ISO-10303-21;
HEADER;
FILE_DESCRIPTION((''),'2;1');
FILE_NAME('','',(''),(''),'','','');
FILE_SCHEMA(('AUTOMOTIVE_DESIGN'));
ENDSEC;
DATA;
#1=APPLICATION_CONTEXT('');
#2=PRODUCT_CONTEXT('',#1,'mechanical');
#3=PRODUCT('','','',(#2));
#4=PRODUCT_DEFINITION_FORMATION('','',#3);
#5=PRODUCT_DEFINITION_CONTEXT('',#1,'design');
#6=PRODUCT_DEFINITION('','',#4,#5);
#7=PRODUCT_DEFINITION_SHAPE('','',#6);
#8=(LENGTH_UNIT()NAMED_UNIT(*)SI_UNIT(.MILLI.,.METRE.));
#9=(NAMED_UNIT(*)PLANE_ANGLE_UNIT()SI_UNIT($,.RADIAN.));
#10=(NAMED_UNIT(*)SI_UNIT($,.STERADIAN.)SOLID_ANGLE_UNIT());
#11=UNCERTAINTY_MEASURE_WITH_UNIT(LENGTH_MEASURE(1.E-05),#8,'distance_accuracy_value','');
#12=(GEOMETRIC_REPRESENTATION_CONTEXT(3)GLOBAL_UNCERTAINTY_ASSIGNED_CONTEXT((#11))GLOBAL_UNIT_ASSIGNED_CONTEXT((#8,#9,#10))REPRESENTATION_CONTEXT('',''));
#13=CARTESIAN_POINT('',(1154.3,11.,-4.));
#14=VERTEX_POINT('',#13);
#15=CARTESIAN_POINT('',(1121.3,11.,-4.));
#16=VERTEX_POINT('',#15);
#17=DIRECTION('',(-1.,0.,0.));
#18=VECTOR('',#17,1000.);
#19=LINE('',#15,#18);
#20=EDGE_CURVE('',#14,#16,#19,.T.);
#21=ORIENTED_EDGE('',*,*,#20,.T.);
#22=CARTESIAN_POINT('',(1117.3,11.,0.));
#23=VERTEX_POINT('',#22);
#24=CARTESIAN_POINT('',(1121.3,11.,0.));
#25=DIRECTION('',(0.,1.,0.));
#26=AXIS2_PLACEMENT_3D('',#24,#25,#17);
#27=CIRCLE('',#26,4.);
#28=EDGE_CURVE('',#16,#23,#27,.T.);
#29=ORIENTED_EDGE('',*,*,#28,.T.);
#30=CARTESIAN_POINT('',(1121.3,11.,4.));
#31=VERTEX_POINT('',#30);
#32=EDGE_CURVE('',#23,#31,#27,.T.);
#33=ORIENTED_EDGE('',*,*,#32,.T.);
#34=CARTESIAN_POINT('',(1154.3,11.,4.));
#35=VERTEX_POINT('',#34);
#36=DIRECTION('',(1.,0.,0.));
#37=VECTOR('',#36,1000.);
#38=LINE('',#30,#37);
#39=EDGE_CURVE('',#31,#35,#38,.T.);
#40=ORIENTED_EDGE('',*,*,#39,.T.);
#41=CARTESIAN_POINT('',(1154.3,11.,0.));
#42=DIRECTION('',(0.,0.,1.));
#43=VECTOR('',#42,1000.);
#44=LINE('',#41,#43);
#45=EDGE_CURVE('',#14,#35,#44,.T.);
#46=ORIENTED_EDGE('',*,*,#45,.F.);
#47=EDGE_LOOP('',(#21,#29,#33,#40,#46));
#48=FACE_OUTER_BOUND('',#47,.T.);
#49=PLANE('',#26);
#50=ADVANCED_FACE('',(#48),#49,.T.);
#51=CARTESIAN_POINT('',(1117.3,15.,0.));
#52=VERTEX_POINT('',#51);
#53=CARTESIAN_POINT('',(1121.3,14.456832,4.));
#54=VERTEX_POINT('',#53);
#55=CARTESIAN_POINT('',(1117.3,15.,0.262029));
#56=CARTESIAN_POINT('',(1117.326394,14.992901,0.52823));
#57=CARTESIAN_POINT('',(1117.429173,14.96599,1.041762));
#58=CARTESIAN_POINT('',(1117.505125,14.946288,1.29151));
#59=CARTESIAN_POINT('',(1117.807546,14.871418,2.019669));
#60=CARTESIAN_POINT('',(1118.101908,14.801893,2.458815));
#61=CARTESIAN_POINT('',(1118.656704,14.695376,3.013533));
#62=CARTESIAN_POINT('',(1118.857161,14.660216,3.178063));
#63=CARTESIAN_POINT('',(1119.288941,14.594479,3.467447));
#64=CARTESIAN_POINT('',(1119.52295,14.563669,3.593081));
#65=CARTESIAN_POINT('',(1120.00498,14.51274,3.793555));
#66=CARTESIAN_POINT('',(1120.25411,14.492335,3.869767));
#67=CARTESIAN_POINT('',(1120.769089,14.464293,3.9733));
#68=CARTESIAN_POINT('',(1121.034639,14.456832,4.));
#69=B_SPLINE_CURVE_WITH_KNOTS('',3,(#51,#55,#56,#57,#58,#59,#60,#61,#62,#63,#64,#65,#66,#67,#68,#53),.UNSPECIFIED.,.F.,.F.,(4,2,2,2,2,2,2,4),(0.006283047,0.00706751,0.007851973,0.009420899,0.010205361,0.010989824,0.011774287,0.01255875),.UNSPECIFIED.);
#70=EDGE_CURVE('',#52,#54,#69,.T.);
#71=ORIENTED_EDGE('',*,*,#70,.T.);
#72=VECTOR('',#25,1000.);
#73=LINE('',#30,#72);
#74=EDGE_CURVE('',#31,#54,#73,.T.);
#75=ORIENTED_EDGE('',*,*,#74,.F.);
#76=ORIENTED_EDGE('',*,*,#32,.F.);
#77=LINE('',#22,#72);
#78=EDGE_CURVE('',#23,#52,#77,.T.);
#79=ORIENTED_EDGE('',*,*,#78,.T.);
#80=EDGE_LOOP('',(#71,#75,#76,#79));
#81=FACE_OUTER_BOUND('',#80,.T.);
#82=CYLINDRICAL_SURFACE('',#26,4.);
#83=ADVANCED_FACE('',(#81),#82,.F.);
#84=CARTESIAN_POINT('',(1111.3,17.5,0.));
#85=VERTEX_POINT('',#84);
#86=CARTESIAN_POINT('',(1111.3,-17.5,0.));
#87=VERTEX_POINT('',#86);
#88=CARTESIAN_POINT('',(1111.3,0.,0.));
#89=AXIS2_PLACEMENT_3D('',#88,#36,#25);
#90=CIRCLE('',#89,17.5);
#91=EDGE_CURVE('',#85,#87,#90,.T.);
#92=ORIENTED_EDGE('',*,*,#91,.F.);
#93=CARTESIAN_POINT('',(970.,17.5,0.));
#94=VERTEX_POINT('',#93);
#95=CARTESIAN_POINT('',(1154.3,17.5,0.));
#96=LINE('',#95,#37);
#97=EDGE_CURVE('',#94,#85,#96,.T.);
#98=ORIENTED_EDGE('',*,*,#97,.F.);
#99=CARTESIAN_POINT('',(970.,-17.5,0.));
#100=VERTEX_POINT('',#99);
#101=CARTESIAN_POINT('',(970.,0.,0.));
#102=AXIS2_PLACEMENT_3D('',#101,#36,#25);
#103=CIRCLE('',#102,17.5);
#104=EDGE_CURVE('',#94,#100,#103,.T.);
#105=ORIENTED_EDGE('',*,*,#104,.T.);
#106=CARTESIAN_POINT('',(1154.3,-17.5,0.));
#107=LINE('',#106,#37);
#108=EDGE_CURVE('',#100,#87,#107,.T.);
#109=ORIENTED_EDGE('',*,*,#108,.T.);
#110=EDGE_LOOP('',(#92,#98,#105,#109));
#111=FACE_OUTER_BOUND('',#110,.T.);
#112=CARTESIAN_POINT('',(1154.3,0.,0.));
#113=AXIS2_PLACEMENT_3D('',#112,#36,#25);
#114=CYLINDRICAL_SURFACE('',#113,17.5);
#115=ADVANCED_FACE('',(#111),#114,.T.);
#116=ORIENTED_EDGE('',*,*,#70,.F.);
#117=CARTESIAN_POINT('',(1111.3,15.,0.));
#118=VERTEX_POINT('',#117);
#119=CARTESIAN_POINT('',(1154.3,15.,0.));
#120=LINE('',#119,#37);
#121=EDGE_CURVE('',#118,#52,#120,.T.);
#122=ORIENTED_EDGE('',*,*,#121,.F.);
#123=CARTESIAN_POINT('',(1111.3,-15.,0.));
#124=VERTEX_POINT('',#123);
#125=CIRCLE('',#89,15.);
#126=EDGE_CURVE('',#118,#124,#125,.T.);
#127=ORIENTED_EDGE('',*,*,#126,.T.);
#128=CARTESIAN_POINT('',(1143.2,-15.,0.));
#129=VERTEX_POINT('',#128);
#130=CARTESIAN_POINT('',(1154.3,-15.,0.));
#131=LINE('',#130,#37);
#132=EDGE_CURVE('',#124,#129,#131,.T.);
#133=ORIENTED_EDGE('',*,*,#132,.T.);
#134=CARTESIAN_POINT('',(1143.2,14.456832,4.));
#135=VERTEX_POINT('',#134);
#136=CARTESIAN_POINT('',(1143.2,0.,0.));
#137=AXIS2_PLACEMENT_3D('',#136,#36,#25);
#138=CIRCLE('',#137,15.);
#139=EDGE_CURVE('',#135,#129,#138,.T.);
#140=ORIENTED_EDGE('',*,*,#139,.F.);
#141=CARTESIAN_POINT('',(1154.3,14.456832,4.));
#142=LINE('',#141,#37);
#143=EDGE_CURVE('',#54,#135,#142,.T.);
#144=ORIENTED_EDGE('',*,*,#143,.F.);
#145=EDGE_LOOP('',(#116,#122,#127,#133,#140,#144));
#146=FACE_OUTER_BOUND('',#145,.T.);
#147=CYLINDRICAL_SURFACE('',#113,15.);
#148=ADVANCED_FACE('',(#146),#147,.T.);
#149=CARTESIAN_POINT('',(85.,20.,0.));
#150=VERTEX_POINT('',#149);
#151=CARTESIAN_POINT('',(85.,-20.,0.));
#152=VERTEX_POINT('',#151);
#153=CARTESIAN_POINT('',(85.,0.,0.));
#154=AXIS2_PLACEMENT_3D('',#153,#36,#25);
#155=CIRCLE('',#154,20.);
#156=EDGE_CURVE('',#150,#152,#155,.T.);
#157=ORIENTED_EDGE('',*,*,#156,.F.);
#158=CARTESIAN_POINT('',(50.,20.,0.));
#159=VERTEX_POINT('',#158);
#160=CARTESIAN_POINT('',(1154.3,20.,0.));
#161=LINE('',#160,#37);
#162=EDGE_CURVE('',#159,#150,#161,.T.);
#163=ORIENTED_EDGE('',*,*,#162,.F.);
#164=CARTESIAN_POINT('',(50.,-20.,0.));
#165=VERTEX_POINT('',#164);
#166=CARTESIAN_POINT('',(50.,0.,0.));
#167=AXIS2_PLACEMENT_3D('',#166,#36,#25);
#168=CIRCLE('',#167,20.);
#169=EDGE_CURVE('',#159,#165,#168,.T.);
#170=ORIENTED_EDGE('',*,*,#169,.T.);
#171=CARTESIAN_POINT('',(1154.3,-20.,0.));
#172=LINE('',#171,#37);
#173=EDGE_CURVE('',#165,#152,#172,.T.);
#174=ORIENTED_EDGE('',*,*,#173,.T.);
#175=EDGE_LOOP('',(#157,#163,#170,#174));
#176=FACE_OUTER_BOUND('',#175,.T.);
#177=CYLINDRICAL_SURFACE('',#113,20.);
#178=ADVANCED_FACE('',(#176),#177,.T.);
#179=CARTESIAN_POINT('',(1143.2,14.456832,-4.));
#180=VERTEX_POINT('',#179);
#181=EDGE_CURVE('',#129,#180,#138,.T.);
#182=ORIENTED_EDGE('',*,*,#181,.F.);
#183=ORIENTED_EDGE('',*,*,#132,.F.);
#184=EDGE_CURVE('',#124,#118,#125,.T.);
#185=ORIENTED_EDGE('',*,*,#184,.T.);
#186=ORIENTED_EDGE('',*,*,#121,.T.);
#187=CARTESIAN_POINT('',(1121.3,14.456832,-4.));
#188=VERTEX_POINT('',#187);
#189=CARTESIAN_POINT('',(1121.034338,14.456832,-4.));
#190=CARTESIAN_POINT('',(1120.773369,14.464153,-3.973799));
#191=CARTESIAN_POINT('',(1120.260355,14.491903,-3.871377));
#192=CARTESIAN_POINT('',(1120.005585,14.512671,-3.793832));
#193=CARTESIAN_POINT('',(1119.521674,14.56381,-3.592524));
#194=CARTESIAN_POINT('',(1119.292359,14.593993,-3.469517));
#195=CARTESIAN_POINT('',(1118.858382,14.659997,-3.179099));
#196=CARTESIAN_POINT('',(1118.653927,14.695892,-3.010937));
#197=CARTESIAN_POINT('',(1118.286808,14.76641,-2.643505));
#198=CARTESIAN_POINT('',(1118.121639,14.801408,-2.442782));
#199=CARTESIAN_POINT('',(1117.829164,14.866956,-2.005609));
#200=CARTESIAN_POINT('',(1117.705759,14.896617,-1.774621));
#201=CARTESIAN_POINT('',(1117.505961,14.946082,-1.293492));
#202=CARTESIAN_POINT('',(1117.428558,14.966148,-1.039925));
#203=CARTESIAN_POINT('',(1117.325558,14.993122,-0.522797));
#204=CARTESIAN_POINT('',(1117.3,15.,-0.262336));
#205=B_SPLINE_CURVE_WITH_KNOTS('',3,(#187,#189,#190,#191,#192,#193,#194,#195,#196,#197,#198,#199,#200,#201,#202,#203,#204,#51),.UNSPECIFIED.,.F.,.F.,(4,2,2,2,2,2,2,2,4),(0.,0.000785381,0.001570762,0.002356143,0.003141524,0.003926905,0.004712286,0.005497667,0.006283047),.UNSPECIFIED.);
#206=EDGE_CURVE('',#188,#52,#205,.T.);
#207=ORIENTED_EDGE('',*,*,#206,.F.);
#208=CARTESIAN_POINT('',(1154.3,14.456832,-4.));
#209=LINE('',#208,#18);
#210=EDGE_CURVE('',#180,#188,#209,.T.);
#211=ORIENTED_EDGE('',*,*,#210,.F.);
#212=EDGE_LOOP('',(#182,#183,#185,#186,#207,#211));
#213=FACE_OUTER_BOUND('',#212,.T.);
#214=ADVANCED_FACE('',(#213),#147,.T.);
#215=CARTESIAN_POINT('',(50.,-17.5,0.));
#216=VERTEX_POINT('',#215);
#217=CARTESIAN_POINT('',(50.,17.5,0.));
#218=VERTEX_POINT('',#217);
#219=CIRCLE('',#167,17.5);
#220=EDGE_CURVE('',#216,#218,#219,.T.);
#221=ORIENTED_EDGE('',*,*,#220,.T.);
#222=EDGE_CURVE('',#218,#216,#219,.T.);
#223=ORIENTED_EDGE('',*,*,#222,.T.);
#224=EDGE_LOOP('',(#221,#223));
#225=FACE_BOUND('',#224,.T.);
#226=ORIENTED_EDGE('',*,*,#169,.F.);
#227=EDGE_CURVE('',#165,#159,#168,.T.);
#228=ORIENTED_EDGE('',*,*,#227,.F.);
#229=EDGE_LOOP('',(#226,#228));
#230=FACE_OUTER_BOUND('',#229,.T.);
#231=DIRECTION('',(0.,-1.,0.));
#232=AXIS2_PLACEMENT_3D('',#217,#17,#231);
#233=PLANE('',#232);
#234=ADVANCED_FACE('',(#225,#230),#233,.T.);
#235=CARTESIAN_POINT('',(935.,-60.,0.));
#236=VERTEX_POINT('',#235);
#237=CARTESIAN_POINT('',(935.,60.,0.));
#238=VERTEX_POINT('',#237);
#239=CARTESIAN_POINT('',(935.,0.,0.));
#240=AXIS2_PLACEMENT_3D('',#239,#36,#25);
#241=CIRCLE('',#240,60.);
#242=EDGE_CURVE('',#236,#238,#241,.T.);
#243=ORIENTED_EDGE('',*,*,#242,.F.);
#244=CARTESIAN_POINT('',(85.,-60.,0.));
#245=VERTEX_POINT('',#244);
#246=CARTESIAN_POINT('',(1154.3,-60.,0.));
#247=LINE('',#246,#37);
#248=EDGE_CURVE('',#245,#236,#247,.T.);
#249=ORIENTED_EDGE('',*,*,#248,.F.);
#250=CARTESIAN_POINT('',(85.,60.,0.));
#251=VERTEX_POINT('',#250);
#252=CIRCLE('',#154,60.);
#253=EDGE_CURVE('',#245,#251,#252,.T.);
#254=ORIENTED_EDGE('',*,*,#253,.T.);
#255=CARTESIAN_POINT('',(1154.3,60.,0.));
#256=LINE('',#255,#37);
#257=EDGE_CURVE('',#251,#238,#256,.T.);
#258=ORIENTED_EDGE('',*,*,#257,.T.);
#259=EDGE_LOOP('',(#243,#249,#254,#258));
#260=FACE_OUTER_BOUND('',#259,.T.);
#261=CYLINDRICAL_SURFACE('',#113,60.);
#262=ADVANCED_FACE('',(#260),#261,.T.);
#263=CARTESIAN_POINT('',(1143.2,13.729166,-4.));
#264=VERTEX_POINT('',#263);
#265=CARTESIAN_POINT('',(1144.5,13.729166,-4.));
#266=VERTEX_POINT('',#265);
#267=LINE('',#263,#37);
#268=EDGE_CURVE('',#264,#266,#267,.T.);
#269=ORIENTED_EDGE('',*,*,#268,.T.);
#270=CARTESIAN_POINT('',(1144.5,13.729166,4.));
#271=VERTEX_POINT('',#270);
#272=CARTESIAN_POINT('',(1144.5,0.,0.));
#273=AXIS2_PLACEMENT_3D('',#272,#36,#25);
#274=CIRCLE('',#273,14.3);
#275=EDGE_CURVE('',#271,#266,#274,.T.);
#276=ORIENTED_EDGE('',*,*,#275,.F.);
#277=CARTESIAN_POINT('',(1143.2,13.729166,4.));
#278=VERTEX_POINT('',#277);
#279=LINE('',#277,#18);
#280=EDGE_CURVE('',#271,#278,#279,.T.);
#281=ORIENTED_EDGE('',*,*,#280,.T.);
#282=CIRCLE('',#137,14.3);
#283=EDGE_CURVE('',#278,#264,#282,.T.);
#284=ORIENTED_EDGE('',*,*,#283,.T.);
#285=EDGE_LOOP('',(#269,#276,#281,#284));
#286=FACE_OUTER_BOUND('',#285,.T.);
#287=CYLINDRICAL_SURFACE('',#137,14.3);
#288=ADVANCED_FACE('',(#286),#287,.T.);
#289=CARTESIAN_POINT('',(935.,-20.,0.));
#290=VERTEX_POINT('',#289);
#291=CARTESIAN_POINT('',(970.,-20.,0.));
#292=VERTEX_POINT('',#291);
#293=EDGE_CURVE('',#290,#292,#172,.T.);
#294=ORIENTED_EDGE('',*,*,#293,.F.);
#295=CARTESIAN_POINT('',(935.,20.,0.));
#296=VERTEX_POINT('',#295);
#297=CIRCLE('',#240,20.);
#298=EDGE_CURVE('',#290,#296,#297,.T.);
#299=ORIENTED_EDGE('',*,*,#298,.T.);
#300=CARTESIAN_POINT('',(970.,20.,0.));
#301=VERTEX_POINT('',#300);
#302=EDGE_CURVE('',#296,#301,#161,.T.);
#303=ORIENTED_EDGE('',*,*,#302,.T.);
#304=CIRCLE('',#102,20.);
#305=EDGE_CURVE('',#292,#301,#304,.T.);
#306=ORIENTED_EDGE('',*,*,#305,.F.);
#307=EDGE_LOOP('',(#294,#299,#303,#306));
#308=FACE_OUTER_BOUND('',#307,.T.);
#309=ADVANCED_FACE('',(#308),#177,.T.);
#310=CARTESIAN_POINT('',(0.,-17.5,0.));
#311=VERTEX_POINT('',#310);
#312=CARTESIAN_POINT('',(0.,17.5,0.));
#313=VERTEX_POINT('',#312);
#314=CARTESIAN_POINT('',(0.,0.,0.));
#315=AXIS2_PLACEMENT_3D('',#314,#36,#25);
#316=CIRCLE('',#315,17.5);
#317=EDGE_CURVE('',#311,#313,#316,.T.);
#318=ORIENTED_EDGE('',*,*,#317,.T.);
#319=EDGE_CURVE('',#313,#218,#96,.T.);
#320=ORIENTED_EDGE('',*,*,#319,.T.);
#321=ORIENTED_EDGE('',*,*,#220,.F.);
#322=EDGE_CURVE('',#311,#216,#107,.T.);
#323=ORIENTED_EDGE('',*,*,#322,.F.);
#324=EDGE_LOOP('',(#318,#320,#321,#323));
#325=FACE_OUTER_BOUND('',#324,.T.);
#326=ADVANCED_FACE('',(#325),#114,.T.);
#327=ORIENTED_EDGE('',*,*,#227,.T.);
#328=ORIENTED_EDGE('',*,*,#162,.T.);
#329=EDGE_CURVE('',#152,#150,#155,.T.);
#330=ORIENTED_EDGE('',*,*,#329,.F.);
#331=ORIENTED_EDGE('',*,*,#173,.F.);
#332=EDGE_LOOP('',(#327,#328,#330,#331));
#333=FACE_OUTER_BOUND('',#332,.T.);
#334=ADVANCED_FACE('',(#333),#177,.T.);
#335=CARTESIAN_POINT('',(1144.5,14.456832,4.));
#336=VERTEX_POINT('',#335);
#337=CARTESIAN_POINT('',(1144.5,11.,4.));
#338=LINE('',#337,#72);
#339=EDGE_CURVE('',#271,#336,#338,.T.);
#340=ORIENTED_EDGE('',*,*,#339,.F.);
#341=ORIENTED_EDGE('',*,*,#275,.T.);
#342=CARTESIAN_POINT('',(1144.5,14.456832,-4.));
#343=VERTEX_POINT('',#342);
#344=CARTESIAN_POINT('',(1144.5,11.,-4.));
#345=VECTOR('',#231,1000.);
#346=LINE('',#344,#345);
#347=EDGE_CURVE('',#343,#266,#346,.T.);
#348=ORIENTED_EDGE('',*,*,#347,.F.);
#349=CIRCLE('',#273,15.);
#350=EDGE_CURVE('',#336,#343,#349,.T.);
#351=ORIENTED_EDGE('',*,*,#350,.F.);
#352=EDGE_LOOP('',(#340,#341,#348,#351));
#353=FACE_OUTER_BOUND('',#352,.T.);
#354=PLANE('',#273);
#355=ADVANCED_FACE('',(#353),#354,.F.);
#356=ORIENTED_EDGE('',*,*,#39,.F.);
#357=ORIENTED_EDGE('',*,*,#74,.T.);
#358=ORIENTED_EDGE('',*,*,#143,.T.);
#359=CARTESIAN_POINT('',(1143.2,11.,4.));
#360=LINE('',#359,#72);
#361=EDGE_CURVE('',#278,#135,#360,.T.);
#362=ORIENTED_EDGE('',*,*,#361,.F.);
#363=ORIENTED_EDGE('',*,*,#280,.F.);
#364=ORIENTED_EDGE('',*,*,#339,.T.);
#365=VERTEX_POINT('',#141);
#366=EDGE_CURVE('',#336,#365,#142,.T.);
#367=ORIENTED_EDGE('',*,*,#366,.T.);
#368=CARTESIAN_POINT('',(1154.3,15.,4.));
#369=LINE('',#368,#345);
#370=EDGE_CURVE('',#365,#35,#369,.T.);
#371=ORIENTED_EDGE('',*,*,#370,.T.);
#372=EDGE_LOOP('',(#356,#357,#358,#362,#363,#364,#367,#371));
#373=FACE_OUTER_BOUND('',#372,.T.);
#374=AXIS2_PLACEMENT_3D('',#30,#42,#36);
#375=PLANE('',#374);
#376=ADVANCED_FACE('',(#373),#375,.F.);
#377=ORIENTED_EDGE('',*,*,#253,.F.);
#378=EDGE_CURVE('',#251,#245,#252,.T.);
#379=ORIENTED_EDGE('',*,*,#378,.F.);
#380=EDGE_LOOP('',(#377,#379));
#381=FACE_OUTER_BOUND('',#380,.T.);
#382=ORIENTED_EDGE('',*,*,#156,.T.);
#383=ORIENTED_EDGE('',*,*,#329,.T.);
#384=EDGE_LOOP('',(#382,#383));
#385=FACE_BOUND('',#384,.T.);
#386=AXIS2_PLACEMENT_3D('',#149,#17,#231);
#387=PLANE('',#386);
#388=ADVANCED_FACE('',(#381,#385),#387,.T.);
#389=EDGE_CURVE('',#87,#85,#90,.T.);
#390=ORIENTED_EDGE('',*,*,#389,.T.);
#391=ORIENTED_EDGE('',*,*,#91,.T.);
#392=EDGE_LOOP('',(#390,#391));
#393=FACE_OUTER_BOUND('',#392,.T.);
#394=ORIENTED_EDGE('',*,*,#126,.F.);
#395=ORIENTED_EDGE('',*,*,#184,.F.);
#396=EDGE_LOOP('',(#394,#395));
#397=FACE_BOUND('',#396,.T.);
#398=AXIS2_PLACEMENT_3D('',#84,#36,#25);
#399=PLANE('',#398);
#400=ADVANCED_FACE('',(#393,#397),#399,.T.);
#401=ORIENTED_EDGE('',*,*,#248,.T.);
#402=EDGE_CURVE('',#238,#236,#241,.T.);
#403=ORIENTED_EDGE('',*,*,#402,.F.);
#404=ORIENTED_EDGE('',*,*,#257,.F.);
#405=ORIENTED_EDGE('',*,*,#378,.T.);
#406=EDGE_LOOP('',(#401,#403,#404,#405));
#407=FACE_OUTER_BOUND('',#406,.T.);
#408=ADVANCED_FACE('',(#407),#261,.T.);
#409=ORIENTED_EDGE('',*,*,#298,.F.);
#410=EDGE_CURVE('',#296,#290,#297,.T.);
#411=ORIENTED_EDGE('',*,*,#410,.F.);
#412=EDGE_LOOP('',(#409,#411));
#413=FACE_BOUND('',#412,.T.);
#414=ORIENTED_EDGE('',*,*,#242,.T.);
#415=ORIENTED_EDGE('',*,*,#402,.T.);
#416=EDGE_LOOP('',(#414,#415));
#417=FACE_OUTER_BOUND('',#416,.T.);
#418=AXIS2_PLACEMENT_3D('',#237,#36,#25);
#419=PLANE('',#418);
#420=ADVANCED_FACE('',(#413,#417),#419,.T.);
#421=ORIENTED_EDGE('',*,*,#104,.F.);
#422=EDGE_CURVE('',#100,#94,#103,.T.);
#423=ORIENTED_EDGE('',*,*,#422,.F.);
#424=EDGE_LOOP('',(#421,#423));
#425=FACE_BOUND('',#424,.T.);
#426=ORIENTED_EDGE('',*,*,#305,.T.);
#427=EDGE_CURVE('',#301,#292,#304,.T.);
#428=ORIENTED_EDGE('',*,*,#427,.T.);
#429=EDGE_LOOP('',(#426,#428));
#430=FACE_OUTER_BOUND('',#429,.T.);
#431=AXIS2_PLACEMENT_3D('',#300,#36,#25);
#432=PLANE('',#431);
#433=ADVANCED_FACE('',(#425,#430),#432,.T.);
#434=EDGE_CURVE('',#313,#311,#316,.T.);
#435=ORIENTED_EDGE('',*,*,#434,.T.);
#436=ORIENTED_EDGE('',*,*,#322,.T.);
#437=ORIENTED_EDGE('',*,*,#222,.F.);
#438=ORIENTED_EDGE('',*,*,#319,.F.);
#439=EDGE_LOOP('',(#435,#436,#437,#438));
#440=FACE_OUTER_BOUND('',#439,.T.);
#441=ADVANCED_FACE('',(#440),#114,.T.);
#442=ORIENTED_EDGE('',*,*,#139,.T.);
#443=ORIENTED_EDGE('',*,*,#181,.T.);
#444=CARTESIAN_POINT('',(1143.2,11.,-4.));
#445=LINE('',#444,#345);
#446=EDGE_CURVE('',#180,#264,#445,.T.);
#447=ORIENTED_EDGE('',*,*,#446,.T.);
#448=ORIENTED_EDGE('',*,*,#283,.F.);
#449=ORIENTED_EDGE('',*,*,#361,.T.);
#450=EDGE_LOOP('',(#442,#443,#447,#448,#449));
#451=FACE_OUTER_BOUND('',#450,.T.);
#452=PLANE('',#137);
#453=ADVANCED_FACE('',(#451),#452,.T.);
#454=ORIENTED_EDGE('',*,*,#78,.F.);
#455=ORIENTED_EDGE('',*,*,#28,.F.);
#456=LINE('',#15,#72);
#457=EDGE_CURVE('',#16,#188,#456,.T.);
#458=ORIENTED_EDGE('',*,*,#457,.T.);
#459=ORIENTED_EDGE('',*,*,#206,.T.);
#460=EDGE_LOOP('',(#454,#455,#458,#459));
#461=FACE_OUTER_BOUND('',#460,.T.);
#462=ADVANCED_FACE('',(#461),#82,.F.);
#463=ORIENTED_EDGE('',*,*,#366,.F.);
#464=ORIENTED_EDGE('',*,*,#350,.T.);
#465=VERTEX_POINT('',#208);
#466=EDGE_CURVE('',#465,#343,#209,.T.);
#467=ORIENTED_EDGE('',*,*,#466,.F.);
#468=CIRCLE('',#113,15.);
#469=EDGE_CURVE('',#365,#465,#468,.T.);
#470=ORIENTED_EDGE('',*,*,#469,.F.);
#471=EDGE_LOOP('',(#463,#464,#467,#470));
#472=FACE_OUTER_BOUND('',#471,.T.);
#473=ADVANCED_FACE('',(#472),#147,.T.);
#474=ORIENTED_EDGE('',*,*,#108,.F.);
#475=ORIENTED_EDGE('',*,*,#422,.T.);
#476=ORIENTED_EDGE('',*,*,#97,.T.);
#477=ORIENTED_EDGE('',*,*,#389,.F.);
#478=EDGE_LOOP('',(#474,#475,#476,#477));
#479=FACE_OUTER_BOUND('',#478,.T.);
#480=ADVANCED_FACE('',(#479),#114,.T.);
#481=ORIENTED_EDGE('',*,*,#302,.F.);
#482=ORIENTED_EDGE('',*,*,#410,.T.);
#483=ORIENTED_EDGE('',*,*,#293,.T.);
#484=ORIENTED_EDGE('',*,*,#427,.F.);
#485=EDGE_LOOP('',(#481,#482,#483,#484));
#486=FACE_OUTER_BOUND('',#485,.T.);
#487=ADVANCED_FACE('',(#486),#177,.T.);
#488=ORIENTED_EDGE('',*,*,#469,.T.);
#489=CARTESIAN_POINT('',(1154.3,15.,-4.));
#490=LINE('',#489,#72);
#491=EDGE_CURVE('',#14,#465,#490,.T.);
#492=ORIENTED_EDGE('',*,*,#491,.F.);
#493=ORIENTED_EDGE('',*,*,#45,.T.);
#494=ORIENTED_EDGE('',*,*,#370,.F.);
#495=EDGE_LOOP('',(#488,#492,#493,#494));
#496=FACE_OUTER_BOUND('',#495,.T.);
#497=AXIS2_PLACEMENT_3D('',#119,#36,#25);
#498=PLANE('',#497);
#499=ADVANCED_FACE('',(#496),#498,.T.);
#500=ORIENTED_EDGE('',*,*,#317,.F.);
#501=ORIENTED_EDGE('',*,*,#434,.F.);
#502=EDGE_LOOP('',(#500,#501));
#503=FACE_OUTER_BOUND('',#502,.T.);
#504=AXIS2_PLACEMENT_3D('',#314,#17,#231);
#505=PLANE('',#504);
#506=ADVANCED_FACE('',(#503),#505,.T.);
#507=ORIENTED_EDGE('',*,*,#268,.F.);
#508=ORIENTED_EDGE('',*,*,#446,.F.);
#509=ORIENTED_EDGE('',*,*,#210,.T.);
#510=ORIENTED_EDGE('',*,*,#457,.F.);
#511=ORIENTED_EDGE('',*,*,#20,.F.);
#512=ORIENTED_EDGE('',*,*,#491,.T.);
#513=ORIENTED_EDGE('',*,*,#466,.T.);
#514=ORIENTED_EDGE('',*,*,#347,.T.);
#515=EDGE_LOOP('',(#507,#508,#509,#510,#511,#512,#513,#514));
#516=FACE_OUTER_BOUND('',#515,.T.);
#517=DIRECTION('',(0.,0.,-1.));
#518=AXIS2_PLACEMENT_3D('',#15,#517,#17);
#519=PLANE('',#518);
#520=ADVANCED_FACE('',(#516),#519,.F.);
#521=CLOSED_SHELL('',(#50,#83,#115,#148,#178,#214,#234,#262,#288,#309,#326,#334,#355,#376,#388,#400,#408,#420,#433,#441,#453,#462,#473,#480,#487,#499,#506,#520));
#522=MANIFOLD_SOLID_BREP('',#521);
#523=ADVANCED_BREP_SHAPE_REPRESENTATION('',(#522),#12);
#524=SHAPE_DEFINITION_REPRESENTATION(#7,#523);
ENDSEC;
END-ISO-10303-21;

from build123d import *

# Parameters (mm, degrees)
CUT_EXTRUDE_1_DEPTH = 4
SKETCH_3_R          = 15
SKETCH_3_R_2        = 14.3
CUT_EXTRUDE_3_DEPTH = 1.3


with BuildPart() as part:
    # 草图1 → 旋转1 (revolve)
    with BuildSketch(Plane.XY):
        Polygon((0, 0), (0, 17.5), (50, 17.5), (50, 20), (85, 20), (85, 60), (935, 60), (935, 20), (970, 20), (970, 17.5), (1111.3, 17.5), (1111.3, 15), (1154.3, 15), (1154.3, 0), align=None)
    revolve(axis=Axis((1154.3, 0, 0), (-1, 0, 0)))

    # 草图2 → 切除-拉伸1 (cut)
    with BuildSketch(Plane(origin=(0, 15, 0), x_dir=(1, 0, 0), z_dir=(0, 1, 0))):
        with BuildLine():
            Line((1121.3, 4), (1164.3, 4))
            Line((1164.3, 4), (1164.3, -4))
            Line((1164.3, -4), (1121.3, -4))
            ThreePointArc((1121.3, -4), (1117.3, 0), (1121.3, 4))
        make_face()
    extrude(amount=-CUT_EXTRUDE_1_DEPTH, mode=Mode.SUBTRACT)

    # 草图3 → 切除-拉伸3 (cut)
    with BuildSketch(Plane(origin=(1144.5, 0, 0), x_dir=(0, 0, -1), z_dir=(1, 0, 0))):
        with Locations(Location((0, 0, 0), (0, 0, 90))):
            Circle(SKETCH_3_R)
        Circle(SKETCH_3_R_2, mode=Mode.SUBTRACT)
    extrude(amount=-CUT_EXTRUDE_3_DEPTH, mode=Mode.SUBTRACT)


solid = part.part
